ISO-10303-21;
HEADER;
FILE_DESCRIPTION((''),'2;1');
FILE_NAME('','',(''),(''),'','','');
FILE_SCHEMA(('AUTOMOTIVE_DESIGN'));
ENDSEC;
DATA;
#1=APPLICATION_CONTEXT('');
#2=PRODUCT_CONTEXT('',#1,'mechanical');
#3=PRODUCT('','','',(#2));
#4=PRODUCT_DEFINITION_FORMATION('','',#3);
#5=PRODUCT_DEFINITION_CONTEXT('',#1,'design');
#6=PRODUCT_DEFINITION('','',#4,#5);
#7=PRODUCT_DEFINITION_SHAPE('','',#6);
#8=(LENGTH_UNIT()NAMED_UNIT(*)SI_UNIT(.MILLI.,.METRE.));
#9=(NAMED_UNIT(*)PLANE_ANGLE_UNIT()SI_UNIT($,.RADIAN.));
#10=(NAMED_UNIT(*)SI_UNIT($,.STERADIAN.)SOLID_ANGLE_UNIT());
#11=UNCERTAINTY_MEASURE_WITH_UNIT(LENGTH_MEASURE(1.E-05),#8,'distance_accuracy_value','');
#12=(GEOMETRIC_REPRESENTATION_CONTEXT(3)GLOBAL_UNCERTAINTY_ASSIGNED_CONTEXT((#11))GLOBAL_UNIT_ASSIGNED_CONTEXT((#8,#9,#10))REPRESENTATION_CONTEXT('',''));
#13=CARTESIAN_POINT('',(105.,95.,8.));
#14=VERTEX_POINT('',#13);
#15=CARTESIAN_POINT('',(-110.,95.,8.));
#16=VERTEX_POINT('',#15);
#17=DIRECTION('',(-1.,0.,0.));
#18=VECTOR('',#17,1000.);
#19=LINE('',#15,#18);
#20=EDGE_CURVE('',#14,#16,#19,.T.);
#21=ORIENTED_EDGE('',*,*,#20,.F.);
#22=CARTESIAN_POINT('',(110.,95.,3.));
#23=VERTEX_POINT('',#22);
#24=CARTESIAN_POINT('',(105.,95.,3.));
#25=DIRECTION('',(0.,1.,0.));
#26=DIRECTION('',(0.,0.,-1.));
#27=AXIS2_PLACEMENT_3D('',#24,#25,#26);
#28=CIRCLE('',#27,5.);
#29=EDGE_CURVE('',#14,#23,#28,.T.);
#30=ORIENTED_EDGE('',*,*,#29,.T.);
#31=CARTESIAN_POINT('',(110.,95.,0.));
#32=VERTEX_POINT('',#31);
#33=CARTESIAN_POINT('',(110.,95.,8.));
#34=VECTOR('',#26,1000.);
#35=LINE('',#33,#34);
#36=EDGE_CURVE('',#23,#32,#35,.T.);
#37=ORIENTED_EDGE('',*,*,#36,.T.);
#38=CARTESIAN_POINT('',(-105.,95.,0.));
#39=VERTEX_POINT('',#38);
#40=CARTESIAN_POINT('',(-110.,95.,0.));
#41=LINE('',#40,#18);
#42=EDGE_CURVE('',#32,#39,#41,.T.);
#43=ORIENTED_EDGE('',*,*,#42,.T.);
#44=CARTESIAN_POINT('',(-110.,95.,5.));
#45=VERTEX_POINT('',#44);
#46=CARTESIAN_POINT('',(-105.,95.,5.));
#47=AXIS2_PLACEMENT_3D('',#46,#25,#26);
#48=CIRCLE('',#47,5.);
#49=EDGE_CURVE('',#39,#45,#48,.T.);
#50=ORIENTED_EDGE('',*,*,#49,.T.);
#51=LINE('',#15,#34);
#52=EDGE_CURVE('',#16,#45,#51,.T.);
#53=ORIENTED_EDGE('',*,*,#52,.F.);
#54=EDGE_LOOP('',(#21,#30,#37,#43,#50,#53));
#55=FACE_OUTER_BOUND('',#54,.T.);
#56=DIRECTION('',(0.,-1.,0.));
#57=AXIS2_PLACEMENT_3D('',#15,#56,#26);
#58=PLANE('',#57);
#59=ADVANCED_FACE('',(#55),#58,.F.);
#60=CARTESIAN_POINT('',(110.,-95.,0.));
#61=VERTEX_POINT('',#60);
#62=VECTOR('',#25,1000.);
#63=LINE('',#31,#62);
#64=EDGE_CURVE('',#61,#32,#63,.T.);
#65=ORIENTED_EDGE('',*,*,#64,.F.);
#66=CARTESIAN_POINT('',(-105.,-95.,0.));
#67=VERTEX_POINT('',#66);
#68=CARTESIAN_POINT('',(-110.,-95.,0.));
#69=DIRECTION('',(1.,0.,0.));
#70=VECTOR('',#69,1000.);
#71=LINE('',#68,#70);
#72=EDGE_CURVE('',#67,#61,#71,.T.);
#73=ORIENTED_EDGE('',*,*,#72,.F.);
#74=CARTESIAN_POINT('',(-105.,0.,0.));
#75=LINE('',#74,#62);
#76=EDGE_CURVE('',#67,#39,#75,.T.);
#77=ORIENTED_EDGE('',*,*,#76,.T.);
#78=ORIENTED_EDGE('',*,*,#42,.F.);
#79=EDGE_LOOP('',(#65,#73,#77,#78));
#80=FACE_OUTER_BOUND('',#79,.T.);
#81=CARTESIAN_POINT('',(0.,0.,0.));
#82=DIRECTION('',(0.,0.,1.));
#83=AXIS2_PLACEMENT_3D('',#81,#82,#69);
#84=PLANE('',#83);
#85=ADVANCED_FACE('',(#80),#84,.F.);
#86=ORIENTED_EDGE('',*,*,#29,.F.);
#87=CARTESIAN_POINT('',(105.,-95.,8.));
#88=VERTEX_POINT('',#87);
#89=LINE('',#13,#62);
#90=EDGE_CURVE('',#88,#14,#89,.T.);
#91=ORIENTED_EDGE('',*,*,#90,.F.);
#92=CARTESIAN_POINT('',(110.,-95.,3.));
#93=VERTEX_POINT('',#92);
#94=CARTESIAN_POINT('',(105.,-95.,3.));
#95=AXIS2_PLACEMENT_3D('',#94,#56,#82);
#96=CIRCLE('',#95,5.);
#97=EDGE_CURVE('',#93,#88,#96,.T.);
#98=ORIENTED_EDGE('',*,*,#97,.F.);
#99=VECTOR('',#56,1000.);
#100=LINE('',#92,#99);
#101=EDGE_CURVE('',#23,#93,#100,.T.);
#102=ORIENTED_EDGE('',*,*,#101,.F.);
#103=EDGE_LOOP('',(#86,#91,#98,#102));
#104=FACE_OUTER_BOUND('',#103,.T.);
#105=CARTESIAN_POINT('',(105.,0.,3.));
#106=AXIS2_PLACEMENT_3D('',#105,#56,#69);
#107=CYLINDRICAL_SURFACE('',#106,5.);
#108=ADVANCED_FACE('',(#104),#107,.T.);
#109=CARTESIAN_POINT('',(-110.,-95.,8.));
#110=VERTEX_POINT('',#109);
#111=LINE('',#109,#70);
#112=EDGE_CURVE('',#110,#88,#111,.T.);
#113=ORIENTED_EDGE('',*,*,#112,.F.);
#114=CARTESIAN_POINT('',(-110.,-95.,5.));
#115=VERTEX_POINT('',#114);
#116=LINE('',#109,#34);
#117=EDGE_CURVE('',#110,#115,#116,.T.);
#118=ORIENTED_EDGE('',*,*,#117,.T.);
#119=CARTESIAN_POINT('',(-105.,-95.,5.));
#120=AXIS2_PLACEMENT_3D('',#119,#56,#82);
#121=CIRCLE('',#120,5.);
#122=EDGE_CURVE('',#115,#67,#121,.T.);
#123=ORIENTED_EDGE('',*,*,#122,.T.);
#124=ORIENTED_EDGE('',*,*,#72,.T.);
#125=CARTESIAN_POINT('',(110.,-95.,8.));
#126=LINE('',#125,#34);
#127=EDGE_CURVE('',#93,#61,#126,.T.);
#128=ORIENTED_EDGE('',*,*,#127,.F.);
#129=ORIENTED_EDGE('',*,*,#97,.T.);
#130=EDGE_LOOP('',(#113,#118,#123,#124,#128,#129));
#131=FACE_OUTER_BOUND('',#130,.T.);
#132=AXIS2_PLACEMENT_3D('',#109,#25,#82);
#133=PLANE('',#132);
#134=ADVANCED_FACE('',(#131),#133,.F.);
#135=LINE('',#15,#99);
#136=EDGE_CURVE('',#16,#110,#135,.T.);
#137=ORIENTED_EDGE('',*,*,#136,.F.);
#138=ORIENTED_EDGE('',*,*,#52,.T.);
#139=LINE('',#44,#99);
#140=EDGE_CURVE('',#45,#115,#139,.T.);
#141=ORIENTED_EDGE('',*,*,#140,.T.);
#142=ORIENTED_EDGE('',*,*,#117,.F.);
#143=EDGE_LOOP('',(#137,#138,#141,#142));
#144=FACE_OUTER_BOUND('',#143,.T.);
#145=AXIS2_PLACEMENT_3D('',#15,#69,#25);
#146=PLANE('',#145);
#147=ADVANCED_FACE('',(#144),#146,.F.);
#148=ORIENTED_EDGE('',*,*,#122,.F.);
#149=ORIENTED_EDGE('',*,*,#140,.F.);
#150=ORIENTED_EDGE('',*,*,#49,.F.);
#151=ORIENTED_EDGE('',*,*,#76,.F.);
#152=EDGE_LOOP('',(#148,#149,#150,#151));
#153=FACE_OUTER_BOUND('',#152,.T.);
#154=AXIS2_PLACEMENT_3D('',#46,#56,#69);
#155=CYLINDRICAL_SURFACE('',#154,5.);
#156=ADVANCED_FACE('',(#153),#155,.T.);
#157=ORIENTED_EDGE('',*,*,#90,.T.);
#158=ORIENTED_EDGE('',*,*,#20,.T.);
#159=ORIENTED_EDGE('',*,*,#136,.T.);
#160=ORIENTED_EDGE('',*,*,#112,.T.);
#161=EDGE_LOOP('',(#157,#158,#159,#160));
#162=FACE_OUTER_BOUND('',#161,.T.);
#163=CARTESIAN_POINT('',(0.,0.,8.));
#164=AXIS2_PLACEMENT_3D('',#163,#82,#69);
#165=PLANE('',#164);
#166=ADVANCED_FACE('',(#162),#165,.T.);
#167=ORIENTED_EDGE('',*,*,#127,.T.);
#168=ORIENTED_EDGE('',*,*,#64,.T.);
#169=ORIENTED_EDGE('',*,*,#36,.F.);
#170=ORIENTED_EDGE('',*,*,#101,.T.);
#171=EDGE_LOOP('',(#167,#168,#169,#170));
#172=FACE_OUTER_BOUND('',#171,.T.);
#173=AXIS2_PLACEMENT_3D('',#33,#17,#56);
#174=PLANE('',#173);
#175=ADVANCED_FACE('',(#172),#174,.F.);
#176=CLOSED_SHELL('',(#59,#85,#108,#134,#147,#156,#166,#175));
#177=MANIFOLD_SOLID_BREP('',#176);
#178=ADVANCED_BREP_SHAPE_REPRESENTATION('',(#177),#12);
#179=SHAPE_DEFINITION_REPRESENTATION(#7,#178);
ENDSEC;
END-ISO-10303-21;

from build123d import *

# Parameters (mm, degrees)
SKETCH1_W           = 220
SKETCH1_H           = 190
BOSS_EXTRUDE1_DEPTH = 8
FILLET1_R           = 5


with BuildPart() as part:
    # Sketch1 → Boss-Extrude1 (new body)
    with BuildSketch(Plane.XY):
        Rectangle(SKETCH1_W, SKETCH1_H)
    extrude(amount=BOSS_EXTRUDE1_DEPTH)

    # Fillet1
    fillet1_edges = [part.edges().sort_by_distance(p)[0] for p in [
        (110, 0, 8),
        (-110, 0, 0),
    ]]
    fillet(fillet1_edges, radius=FILLET1_R)


solid = part.part
